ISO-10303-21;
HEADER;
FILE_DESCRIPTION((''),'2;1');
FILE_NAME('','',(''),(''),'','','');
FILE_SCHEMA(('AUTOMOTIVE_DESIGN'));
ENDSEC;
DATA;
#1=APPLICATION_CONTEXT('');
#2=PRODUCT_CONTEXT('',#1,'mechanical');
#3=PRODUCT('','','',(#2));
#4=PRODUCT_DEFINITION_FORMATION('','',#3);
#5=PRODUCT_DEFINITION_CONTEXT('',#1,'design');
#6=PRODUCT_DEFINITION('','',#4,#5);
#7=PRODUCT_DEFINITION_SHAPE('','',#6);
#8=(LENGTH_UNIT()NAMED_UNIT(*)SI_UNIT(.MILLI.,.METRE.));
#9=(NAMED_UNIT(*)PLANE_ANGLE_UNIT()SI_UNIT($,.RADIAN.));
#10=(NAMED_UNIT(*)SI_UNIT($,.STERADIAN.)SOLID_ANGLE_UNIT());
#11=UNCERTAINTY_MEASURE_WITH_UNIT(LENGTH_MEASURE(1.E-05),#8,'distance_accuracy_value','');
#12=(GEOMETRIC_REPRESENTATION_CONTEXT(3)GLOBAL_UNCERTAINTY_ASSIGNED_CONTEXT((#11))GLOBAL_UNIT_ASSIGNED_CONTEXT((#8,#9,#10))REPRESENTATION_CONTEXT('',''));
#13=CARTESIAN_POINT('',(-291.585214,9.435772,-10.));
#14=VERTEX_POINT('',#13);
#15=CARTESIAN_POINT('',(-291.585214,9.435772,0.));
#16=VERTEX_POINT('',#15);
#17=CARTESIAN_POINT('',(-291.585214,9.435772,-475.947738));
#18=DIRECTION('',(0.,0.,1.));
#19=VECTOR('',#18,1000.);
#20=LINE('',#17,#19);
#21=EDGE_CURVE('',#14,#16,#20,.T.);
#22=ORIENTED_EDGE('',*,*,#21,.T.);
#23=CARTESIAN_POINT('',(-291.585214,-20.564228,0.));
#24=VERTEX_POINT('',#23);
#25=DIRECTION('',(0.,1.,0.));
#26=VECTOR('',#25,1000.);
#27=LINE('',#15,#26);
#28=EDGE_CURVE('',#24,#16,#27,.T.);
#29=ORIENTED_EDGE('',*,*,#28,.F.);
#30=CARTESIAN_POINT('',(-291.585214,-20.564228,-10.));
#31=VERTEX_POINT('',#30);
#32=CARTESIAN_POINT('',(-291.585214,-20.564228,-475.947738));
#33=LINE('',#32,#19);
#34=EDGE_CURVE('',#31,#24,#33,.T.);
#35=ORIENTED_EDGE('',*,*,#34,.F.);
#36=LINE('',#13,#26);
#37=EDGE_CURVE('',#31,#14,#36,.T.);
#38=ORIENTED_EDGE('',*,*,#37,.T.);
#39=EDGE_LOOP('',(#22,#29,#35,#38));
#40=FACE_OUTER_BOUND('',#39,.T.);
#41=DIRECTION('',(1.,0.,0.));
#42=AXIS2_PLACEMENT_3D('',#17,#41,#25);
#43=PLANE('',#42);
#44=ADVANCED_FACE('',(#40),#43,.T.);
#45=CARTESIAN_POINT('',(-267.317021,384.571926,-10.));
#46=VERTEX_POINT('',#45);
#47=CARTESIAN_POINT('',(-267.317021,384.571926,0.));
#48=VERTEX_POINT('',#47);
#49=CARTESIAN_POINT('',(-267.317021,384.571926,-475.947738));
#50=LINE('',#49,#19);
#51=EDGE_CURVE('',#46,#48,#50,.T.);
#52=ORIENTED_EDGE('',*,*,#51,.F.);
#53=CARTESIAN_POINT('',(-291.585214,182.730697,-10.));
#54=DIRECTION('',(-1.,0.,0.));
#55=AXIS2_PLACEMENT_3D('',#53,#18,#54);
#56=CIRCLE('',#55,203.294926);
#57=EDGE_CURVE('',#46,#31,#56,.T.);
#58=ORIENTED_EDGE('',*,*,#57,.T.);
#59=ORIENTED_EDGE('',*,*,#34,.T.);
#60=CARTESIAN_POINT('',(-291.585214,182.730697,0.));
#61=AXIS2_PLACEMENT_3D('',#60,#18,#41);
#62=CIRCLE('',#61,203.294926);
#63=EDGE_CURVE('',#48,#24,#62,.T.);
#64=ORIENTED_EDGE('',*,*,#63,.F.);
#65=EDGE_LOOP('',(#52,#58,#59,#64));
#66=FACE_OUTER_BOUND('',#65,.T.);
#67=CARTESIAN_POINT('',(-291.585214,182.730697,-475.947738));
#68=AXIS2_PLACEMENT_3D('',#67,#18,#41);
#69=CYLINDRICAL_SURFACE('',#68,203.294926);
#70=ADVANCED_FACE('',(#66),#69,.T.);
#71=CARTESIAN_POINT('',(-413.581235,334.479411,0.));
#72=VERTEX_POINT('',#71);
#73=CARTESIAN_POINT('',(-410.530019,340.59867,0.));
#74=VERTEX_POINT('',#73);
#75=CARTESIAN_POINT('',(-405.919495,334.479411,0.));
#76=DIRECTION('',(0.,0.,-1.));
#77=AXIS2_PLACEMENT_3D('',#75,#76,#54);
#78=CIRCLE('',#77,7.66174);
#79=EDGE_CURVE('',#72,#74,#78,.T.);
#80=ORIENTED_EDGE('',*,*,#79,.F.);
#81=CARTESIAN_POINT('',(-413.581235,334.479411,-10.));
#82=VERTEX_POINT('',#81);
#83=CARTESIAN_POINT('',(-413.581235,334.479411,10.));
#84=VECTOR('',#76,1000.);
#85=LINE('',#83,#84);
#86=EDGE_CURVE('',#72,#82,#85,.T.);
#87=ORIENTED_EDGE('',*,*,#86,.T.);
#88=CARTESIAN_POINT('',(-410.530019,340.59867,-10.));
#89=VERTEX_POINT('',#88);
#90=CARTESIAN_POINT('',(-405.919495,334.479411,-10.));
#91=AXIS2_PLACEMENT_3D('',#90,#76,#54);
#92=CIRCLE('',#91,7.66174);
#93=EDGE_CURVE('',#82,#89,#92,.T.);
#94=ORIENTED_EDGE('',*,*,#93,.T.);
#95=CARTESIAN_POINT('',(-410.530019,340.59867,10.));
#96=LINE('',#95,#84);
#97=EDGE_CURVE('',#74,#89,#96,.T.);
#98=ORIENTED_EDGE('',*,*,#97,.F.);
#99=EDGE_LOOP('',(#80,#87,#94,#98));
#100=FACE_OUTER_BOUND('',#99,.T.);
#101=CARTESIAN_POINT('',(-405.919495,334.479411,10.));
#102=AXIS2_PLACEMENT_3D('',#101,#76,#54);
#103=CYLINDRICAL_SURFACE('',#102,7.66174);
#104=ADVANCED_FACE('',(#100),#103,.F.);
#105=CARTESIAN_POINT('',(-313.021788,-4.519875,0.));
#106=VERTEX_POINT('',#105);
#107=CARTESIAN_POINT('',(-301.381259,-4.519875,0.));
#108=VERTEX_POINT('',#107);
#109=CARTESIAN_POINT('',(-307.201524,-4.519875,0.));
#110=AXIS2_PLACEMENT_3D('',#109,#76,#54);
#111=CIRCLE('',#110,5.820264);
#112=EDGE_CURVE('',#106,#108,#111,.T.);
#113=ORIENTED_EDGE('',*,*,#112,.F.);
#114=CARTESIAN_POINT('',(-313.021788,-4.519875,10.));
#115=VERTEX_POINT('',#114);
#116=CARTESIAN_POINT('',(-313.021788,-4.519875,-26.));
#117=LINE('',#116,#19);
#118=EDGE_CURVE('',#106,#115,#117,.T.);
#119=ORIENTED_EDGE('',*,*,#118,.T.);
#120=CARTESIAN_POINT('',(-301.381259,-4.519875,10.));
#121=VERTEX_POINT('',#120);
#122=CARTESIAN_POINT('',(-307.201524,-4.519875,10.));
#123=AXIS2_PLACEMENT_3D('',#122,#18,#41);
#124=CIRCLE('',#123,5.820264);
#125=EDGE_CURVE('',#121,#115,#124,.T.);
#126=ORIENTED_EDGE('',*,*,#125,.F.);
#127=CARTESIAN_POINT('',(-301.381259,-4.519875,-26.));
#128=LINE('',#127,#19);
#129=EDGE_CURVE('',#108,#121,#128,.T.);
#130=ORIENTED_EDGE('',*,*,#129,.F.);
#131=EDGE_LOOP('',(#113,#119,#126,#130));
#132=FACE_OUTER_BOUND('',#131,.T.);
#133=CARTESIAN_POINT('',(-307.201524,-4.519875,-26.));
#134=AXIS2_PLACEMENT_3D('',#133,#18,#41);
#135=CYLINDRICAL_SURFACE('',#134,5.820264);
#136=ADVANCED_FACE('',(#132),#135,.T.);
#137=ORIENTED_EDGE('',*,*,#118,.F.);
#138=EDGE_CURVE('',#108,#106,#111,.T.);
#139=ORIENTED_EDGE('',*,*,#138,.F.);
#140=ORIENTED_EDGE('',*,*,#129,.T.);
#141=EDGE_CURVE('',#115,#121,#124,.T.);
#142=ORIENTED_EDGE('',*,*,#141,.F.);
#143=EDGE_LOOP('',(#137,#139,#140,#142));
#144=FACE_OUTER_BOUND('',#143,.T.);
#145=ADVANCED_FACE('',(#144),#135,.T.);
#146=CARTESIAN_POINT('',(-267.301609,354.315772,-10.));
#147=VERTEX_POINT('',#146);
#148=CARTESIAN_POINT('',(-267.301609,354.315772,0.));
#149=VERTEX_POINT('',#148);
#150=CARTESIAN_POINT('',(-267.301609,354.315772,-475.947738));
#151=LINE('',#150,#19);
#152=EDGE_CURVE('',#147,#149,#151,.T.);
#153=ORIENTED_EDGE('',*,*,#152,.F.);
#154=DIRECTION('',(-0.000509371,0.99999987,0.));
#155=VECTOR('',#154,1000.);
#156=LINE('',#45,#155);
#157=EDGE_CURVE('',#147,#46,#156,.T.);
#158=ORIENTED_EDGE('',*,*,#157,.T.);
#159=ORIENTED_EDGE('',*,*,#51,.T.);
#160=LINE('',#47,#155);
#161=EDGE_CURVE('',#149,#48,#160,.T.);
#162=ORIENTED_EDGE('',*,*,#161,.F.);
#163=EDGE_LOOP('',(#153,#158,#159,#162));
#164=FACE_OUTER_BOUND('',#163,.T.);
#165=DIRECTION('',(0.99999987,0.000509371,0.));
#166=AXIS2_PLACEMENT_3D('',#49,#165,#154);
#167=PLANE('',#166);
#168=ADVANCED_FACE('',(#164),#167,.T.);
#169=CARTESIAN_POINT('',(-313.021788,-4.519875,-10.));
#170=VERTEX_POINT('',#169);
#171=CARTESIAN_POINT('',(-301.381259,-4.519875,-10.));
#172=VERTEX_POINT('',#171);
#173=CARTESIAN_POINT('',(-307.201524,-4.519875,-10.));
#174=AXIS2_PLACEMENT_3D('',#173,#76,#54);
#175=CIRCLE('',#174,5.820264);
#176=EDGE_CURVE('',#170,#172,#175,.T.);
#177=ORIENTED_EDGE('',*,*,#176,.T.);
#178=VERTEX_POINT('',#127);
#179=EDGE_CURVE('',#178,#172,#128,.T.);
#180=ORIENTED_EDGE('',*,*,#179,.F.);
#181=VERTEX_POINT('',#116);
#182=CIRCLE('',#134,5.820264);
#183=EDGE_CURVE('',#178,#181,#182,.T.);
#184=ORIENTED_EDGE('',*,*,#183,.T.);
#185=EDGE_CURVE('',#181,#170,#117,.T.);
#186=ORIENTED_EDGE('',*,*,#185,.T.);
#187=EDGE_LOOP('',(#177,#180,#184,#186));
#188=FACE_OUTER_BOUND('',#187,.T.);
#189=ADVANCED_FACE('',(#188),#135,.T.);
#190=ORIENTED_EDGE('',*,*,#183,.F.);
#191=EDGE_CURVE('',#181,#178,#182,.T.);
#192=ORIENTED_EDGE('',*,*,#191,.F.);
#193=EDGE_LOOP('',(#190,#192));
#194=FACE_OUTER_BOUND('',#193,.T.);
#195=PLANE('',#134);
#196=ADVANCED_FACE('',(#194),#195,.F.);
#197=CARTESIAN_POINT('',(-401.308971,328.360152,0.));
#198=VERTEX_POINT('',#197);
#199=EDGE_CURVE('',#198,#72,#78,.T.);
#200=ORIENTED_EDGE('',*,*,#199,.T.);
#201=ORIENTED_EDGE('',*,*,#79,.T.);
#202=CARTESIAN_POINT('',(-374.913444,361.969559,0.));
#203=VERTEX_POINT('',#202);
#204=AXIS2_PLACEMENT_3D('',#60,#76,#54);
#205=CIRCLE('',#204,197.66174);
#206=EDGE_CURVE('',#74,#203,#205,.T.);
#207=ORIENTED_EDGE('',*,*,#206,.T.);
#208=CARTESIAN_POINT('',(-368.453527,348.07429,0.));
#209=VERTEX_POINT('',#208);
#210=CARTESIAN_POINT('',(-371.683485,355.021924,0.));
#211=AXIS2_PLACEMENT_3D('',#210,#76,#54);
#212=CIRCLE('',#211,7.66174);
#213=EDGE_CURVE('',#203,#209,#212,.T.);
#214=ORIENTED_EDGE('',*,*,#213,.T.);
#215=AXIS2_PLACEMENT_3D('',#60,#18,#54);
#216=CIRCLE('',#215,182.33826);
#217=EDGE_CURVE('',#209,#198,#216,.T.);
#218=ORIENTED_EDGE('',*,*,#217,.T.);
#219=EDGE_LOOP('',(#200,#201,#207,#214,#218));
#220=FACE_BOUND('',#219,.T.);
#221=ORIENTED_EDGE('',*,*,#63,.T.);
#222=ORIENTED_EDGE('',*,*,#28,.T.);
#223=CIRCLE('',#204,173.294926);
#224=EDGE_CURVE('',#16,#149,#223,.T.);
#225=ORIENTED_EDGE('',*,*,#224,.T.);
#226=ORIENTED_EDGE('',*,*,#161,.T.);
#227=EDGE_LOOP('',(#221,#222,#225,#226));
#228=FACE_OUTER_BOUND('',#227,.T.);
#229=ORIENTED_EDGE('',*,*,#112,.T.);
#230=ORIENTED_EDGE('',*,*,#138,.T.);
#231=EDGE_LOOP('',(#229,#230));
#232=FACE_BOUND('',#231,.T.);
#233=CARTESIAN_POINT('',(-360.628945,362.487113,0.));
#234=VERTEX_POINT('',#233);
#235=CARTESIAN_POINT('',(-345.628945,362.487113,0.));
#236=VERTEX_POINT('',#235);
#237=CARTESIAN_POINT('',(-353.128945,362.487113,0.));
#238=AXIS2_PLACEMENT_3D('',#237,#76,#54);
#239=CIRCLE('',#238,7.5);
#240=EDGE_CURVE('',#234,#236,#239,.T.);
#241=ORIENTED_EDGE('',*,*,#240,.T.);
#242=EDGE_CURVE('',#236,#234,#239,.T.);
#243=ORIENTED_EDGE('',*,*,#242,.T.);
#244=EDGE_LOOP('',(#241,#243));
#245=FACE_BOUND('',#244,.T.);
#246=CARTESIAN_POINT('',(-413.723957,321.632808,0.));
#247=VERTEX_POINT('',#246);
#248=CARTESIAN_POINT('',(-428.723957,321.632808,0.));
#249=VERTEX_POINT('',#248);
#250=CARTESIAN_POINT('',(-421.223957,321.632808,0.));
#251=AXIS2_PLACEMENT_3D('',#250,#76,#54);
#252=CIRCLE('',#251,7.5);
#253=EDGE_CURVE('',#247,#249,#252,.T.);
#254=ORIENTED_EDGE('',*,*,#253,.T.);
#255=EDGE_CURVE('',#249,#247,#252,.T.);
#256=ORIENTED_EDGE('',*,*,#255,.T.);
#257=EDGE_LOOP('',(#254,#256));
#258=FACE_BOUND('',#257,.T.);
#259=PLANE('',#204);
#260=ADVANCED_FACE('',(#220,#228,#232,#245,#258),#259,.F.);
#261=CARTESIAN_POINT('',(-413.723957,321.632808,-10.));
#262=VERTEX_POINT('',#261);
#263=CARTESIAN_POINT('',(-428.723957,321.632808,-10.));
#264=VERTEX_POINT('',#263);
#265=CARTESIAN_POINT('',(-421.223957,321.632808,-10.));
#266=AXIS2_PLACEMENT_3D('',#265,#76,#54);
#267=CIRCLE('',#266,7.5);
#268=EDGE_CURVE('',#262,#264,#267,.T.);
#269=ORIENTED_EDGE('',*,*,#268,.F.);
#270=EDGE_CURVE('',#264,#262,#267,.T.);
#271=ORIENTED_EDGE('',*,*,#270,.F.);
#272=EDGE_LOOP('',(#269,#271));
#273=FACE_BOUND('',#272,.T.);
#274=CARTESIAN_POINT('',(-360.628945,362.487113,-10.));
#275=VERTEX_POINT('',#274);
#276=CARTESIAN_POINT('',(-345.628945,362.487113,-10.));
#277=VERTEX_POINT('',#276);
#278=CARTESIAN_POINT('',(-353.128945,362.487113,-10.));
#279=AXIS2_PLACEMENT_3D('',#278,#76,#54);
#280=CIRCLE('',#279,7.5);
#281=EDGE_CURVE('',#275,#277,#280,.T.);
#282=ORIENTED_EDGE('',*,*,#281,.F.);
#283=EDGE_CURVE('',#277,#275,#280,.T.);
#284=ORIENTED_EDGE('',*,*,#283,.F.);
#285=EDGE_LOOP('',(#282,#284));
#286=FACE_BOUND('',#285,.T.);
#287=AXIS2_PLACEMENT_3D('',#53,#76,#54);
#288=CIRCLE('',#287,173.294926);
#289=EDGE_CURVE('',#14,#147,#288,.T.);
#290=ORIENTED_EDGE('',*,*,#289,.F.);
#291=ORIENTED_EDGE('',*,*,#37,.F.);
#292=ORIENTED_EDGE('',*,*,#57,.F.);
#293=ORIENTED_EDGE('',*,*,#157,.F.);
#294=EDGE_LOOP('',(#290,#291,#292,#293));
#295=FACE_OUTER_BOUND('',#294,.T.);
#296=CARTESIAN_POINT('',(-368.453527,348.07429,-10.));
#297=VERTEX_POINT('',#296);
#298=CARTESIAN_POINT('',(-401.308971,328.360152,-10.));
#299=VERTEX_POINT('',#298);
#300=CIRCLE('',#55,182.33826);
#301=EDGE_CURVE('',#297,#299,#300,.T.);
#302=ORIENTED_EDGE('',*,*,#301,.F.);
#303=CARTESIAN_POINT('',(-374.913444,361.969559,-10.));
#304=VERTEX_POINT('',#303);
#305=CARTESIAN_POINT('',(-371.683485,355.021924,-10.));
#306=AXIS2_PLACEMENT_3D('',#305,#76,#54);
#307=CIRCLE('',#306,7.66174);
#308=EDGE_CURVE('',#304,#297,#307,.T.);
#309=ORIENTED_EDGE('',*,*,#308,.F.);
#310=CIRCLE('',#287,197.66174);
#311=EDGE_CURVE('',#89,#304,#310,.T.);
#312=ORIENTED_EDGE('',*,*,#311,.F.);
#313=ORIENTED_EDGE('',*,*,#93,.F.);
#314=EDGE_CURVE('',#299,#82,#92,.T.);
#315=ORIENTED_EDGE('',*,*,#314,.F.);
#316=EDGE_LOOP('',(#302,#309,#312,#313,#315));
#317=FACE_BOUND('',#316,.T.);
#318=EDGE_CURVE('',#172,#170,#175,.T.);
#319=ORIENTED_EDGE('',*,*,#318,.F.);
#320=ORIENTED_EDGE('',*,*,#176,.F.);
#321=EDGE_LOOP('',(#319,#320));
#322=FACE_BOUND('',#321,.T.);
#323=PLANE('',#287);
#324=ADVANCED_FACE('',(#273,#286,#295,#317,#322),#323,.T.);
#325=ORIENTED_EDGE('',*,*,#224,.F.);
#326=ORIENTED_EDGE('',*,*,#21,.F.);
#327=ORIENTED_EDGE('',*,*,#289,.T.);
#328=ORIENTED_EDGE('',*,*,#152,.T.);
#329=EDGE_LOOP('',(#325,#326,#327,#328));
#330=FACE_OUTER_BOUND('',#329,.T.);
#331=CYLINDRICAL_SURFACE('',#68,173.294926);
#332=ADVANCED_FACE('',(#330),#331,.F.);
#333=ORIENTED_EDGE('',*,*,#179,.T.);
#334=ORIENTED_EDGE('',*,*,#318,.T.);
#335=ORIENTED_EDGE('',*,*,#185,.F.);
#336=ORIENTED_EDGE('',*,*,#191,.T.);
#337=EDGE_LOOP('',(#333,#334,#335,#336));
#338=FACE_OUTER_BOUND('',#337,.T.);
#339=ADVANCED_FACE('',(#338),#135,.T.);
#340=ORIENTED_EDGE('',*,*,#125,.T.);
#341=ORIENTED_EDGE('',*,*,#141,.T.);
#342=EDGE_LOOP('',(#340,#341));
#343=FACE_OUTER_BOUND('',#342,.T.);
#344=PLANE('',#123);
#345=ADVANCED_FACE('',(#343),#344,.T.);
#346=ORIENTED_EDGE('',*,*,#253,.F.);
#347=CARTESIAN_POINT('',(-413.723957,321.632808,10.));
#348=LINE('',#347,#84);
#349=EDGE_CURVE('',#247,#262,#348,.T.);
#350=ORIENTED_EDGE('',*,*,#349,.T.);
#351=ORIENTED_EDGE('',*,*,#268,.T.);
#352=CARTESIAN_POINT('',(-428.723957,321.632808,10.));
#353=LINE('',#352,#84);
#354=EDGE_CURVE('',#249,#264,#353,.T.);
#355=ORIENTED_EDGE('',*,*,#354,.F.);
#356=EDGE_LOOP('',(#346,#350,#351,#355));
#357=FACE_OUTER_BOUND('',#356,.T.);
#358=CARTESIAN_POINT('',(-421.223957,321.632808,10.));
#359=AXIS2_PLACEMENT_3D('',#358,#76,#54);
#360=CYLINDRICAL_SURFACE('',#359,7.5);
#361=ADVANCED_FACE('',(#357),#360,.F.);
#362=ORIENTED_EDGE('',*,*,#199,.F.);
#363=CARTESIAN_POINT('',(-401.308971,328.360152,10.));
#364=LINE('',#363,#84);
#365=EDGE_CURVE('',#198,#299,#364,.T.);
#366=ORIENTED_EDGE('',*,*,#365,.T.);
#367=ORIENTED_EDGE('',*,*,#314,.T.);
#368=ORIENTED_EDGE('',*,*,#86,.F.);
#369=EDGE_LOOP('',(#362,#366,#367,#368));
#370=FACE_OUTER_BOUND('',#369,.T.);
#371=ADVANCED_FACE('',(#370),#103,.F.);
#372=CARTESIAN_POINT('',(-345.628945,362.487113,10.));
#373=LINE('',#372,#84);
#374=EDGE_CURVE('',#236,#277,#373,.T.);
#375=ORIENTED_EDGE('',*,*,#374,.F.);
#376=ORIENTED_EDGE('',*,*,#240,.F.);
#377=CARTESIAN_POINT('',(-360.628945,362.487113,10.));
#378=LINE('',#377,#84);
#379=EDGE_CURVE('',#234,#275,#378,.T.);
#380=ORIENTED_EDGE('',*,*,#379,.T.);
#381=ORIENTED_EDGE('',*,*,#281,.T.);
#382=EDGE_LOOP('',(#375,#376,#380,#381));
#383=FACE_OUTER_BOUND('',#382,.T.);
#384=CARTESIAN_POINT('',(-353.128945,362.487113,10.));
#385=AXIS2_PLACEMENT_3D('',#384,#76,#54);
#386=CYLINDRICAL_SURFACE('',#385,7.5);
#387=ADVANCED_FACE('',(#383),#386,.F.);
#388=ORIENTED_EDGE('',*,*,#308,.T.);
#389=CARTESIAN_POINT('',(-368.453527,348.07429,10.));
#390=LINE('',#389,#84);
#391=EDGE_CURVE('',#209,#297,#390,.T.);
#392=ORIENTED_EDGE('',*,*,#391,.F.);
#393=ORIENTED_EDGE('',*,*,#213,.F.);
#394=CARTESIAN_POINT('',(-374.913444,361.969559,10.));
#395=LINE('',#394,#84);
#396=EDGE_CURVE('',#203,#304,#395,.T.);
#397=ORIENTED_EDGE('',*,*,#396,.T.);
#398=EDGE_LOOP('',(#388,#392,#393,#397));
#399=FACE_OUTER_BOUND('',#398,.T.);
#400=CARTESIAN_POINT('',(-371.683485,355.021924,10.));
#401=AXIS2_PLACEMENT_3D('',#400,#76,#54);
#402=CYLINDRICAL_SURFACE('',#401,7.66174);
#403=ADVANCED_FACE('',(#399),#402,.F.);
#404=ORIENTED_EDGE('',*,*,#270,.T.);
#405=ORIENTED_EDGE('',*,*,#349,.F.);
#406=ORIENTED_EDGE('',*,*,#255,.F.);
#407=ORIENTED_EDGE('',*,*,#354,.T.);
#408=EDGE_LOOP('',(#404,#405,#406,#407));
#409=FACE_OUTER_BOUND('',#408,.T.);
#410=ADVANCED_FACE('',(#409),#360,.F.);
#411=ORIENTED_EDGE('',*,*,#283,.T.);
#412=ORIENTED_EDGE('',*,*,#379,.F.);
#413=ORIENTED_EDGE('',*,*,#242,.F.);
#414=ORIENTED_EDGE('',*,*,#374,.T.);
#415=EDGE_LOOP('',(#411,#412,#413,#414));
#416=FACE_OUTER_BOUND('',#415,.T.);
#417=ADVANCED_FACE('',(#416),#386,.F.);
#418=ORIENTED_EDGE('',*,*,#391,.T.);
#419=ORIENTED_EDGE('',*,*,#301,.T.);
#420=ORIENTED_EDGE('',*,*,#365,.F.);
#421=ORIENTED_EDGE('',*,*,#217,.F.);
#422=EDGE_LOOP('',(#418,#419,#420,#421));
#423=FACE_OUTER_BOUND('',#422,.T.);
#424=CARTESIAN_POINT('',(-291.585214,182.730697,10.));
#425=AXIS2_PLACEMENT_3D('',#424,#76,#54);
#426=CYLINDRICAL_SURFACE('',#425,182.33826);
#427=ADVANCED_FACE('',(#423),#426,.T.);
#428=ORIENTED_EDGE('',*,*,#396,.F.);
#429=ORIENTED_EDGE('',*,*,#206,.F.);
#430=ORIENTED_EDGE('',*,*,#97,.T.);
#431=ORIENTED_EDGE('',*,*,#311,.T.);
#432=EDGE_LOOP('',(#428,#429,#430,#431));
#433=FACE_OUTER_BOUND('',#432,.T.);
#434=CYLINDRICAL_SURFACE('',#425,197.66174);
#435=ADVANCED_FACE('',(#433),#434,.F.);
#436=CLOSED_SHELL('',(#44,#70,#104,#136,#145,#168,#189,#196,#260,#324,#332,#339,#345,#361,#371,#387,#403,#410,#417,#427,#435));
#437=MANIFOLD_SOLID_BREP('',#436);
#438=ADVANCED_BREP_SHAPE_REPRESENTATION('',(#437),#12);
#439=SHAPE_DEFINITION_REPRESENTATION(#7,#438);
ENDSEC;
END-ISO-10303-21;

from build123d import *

# Parameters (mm, degrees)
BOSS_EXTRUDE1_DEPTH      = 10
BOSS_EXTRUDE2_DEPTH      = 10
BOSS_EXTRUDE2_DEPTH_BACK = 26
SKETCH2_R                = 5.820264096
CUT_EXTRUDE4_DEPTH       = 628.950741751
CUT_EXTRUDE4_DEPTH_BACK  = 628.950741751
SKETCH7_R                = 7.5


with BuildPart() as part:
    # Sketch1 → Boss-Extrude1 (new body)
    with BuildSketch(Plane.XY):
        with BuildLine():
            Line((-267.317020812, 384.57192575), (-267.301609192, 354.315771574))
            ThreePointArc((-267.301609192, 354.315771574), (-464.45214838, 194.902560898), (-291.585214163, 9.435771703))
            Line((-291.585214163, 9.435771703), (-291.585214163, -20.564228297))
            ThreePointArc((-291.585214163, -20.564228297), (-494.516390011, 194.886544), (-267.317020812, 384.57192575))
        make_face()
    extrude(amount=-BOSS_EXTRUDE1_DEPTH)

    # Sketch2 → Boss-Extrude2 (add, two sides: drawn at the far end of the back side and taken through both)
    with BuildSketch(Plane.XY.offset(-BOSS_EXTRUDE2_DEPTH_BACK)):
        with Locations((-307.201523558, -4.519874966)):
            Circle(SKETCH2_R)
    extrude(amount=BOSS_EXTRUDE2_DEPTH + BOSS_EXTRUDE2_DEPTH_BACK)

    # Sketch7 → Cut-Extrude4 (cut, two sides: drawn at the far end of the back side and taken through both)
    with BuildSketch(Plane(origin=(0, 0, -10), x_dir=(-1, 0, 0), z_dir=(0, 0, -1)).offset(-CUT_EXTRUDE4_DEPTH_BACK)):
        with Locations((421.223956701, 321.632808197)):
            Circle(SKETCH7_R)
        with Locations((353.128945359, 362.487113382)):
            Circle(SKETCH7_R)
        with BuildLine():
            ThreePointArc((410.530018999, 340.598670168), (393.284643136, 352.222259331), (374.913443912, 361.969559097))
            ThreePointArc((374.913443912, 361.969559097), (364.73585061, 358.251882975), (368.453526733, 348.074289673))
            ThreePointArc((368.453526733, 348.074289673), (385.400521629, 339.082637175), (401.308971217, 328.360152279))
            ThreePointArc((401.308971217, 328.360152279), (412.038754052, 329.868887332), (410.530018999, 340.598670168))
        make_face()
    extrude(amount=CUT_EXTRUDE4_DEPTH + CUT_EXTRUDE4_DEPTH_BACK, mode=Mode.SUBTRACT)


solid = part.part
